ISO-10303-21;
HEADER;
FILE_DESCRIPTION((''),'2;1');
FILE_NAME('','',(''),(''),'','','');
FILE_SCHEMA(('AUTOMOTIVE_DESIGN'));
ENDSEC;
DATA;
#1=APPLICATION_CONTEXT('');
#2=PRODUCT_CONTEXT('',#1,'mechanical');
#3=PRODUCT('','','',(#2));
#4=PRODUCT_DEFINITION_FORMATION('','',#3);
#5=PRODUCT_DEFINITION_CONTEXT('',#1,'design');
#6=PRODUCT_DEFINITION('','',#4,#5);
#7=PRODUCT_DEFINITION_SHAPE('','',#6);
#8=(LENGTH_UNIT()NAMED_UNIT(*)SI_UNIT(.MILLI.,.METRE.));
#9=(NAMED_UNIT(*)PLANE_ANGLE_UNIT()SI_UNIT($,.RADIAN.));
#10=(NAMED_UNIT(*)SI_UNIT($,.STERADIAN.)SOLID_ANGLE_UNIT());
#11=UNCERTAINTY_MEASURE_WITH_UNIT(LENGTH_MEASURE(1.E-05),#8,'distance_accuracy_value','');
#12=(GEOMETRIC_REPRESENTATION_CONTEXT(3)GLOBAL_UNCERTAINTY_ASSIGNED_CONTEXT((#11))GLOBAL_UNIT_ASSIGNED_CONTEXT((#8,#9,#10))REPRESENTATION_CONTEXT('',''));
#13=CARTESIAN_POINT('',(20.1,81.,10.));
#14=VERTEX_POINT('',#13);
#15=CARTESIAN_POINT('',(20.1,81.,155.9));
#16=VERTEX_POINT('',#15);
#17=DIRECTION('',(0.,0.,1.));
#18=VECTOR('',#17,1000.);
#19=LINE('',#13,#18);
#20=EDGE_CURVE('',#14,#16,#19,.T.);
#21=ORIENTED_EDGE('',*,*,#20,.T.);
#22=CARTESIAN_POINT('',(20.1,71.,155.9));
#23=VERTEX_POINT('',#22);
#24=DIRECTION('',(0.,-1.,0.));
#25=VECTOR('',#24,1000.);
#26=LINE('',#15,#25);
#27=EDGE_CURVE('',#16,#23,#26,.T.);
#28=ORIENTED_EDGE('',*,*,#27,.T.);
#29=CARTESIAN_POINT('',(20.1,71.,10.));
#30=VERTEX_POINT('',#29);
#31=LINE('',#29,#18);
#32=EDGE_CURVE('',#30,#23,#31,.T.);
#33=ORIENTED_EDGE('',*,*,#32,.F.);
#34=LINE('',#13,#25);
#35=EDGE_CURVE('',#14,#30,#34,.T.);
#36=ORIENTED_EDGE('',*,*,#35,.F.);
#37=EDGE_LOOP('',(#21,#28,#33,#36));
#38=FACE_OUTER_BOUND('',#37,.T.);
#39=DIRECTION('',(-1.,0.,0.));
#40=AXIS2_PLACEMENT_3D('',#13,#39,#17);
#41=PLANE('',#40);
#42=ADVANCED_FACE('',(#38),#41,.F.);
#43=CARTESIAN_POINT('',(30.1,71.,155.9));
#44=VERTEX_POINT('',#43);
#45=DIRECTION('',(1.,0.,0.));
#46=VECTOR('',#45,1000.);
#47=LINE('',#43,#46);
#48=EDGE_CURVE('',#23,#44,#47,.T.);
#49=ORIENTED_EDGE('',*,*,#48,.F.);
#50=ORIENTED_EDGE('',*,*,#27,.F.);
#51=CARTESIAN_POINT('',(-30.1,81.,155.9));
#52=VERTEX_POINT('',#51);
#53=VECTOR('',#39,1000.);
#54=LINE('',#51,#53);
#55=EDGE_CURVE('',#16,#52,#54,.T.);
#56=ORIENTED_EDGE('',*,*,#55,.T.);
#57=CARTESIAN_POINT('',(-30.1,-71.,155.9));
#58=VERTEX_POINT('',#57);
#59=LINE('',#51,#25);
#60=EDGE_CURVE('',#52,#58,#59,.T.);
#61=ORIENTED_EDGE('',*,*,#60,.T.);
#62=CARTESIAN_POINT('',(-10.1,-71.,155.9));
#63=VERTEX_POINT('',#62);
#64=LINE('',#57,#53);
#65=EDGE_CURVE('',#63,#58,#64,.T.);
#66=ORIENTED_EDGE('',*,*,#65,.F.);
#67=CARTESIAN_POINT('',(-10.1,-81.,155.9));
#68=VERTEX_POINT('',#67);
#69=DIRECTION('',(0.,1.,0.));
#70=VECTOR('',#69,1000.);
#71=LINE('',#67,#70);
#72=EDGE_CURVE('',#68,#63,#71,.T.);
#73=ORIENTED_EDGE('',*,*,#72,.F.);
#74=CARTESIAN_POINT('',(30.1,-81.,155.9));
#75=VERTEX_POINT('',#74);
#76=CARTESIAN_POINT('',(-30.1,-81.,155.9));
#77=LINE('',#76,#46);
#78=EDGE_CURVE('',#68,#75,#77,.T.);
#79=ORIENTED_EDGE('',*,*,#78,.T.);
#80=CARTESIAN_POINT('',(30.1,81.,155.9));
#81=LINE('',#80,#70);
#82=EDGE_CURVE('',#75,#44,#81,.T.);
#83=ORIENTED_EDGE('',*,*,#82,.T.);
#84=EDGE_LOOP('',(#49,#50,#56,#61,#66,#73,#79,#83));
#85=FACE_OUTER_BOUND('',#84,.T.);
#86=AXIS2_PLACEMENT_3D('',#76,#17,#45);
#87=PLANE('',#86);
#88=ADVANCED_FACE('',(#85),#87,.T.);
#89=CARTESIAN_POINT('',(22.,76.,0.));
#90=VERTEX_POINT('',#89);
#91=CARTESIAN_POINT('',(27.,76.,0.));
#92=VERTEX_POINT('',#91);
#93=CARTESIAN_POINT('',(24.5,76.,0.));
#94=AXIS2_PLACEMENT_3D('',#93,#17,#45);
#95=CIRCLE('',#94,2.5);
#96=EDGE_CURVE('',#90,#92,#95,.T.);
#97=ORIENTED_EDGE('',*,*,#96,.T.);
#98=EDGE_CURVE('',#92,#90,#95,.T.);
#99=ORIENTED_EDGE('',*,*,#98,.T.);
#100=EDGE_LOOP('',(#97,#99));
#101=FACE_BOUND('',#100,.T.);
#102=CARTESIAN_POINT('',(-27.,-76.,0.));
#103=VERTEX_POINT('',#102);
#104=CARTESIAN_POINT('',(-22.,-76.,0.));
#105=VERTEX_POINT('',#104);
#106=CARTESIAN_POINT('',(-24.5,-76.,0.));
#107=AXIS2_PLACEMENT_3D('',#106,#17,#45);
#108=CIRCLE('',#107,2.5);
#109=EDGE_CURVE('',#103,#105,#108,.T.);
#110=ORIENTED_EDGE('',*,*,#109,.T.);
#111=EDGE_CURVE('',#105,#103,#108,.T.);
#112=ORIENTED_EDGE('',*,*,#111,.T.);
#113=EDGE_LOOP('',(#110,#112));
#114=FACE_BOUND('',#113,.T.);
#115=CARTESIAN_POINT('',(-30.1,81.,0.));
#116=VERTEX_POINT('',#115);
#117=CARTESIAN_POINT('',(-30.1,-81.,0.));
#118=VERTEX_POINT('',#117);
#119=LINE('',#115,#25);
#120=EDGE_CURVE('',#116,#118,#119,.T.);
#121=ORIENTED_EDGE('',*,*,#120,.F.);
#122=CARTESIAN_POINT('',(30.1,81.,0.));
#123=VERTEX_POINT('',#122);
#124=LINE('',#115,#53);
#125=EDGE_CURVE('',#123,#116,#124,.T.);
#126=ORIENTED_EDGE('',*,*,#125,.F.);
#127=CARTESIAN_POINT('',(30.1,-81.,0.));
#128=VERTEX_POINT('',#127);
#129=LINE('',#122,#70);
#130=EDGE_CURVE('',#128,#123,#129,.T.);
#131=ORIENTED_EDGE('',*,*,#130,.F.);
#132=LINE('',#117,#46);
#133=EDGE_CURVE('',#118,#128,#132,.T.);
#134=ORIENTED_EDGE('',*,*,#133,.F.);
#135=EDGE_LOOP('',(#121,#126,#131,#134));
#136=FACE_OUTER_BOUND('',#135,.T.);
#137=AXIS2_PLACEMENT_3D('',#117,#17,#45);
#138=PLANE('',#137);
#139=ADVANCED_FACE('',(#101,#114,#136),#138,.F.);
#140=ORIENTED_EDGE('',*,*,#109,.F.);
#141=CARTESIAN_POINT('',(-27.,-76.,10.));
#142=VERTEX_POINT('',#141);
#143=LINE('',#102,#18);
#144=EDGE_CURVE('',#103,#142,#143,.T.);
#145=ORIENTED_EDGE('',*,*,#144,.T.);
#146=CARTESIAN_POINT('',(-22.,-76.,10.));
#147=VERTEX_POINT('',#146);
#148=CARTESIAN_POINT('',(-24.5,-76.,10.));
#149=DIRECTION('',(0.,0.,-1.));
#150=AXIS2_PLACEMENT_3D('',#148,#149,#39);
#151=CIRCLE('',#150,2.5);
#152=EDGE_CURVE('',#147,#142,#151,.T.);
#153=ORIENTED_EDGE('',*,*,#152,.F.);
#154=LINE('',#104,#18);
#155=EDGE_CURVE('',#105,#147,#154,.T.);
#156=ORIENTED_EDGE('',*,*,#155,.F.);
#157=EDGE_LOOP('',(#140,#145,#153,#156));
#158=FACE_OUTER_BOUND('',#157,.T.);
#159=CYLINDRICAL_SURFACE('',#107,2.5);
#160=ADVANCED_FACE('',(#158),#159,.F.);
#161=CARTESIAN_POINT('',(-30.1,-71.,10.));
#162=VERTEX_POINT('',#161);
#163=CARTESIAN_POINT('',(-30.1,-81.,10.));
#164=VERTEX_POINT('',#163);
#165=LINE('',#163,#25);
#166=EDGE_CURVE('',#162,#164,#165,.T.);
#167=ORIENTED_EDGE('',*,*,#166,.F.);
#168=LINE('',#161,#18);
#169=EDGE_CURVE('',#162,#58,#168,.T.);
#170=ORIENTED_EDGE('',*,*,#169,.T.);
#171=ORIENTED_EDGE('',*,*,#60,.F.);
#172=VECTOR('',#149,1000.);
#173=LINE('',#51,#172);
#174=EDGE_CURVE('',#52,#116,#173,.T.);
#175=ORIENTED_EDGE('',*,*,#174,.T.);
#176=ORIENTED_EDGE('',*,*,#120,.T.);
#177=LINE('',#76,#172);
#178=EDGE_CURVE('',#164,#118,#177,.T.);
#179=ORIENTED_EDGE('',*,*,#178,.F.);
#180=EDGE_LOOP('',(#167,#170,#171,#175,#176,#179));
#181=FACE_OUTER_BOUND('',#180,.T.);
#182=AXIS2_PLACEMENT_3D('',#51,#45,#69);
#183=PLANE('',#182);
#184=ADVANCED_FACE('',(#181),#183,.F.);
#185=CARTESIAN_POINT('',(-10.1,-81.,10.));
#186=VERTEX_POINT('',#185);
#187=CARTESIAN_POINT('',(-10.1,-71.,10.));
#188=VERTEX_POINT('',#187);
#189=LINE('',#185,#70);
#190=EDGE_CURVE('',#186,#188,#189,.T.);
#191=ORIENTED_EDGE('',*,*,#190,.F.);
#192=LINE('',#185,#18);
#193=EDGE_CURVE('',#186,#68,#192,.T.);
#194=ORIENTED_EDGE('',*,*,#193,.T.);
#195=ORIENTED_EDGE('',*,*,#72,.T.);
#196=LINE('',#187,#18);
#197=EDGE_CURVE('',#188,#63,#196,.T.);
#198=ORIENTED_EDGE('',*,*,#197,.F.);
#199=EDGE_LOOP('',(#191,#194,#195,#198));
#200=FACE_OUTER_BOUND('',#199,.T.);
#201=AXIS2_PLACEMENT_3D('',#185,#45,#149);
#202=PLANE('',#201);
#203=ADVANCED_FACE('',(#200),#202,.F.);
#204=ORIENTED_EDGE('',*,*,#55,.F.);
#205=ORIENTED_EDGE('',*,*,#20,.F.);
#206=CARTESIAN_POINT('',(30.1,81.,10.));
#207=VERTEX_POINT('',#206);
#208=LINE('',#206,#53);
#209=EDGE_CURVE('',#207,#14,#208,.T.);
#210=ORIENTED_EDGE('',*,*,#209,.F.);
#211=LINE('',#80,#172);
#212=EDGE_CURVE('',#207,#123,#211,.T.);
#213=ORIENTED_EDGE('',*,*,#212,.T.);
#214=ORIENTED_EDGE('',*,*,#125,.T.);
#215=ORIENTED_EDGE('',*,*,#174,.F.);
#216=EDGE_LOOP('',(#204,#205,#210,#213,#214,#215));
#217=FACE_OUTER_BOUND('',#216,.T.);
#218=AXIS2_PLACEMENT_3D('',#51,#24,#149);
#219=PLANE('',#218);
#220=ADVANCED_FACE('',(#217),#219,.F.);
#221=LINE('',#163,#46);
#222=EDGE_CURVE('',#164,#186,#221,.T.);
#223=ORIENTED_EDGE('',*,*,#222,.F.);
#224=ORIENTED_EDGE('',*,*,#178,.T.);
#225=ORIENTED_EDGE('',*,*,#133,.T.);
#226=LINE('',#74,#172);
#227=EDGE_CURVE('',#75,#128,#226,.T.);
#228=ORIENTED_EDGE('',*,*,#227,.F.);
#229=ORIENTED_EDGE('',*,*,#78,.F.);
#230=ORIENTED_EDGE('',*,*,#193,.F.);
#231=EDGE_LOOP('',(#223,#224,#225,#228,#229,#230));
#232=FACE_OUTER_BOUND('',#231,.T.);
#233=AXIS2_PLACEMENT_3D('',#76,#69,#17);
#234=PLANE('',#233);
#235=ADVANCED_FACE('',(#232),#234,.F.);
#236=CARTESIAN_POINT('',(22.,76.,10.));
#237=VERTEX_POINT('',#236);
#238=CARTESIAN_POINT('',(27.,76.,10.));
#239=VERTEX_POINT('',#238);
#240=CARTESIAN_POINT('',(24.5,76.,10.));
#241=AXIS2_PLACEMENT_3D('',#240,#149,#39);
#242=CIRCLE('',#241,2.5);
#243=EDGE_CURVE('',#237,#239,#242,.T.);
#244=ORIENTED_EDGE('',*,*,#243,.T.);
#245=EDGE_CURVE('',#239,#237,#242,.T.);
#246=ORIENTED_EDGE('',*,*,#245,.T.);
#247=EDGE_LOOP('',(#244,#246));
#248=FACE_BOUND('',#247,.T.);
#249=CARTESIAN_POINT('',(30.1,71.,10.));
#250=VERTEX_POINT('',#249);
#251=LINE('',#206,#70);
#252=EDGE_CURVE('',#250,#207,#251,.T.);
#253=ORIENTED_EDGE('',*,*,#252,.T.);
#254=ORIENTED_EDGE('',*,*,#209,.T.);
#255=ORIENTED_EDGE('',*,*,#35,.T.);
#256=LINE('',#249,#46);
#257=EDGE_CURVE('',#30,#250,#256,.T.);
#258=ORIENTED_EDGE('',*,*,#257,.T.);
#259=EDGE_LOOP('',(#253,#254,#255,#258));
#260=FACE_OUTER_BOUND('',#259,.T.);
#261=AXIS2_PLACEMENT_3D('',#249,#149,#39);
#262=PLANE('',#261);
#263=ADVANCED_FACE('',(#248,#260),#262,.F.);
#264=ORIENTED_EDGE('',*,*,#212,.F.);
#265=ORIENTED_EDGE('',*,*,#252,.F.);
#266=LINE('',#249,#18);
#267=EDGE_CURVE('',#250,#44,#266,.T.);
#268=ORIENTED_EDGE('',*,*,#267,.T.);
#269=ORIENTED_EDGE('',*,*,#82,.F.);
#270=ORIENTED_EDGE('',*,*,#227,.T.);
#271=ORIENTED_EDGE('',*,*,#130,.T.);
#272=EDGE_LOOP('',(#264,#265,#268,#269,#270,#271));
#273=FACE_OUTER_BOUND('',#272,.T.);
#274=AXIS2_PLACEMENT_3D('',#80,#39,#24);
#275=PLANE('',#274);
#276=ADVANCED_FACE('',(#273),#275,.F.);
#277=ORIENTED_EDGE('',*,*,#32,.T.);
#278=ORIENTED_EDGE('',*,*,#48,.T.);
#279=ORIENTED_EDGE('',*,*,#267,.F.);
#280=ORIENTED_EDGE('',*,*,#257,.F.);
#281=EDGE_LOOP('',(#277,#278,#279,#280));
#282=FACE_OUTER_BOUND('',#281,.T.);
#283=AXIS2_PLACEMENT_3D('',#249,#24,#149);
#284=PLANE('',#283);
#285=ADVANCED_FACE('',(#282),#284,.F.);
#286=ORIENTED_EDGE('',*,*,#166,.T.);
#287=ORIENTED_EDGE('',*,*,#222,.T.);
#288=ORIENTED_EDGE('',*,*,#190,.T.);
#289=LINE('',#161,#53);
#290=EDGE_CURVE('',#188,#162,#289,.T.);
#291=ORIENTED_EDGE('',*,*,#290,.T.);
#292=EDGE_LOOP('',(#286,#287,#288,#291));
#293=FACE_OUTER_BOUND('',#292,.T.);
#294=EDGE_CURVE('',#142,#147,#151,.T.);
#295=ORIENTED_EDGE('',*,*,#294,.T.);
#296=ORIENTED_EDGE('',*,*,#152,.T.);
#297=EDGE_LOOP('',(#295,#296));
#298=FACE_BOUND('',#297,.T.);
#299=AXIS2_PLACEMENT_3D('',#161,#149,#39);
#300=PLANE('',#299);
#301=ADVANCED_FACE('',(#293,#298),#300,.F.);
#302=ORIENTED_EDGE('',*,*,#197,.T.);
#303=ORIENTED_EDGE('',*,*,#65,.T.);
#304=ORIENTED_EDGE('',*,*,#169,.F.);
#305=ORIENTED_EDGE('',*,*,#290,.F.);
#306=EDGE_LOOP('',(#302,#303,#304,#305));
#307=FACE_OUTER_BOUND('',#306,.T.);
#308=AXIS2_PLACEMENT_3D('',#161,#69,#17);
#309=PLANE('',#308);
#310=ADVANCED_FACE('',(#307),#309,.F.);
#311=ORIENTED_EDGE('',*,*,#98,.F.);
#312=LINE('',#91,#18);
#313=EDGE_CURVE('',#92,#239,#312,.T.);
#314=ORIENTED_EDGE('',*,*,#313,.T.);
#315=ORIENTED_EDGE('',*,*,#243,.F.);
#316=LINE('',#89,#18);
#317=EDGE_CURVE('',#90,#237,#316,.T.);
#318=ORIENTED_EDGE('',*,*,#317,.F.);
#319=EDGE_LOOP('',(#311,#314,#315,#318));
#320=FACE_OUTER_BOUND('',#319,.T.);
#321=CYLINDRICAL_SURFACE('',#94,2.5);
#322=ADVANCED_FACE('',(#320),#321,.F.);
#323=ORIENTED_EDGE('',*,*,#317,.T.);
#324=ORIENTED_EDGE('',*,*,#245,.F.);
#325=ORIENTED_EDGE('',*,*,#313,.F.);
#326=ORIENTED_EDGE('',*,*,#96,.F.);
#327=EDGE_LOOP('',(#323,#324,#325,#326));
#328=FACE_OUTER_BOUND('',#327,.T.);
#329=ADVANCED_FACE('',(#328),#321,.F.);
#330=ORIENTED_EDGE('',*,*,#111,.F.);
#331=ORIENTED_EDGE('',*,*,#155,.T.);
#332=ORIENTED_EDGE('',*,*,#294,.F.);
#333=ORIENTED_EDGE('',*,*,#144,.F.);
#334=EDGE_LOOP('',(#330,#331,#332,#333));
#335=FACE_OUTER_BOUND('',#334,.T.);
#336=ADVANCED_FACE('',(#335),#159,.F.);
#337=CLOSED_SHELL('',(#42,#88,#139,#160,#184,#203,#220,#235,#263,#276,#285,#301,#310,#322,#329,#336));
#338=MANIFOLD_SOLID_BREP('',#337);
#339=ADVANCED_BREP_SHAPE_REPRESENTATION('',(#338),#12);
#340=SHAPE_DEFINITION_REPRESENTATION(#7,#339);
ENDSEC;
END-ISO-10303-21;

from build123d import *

# Parameters (mm, degrees)
SKETCH1_W          = 60.2
SKETCH1_H          = 162
EXTRUDE1_DEPTH     = 155.9
SKETCH2_W          = 20
SKETCH2_H          = 10
SKETCH2_W_2        = 10
CUT_EXTRUDE1_DEPTH = 145.9
SKETCH3_R          = 2.5
CUT_EXTRUDE2_DEPTH = 179.246514692


with BuildPart() as part:
    # Sketch1 → Extrude1 (new body)
    with BuildSketch(Plane.XY):
        Rectangle(SKETCH1_W, SKETCH1_H)
    extrude(amount=EXTRUDE1_DEPTH)

    # Sketch2 → Cut-Extrude1 (cut)
    with BuildSketch(Plane.XY.offset(155.9)):
        with Locations((-20.1, -76)):
            Rectangle(SKETCH2_W, SKETCH2_H)
        with Locations((25.1, 76)):
            Rectangle(SKETCH2_W_2, SKETCH2_H)
    extrude(amount=-CUT_EXTRUDE1_DEPTH, mode=Mode.SUBTRACT)

    # Sketch3 → Cut-Extrude2 (cut, through all)
    with BuildSketch(Plane.XY.offset(155.9)):
        with Locations((24.5, 76)):
            Circle(SKETCH3_R)
        with Locations((-24.5, -76)):
            Circle(SKETCH3_R)
    extrude(amount=-CUT_EXTRUDE2_DEPTH, mode=Mode.SUBTRACT)


solid = part.part
